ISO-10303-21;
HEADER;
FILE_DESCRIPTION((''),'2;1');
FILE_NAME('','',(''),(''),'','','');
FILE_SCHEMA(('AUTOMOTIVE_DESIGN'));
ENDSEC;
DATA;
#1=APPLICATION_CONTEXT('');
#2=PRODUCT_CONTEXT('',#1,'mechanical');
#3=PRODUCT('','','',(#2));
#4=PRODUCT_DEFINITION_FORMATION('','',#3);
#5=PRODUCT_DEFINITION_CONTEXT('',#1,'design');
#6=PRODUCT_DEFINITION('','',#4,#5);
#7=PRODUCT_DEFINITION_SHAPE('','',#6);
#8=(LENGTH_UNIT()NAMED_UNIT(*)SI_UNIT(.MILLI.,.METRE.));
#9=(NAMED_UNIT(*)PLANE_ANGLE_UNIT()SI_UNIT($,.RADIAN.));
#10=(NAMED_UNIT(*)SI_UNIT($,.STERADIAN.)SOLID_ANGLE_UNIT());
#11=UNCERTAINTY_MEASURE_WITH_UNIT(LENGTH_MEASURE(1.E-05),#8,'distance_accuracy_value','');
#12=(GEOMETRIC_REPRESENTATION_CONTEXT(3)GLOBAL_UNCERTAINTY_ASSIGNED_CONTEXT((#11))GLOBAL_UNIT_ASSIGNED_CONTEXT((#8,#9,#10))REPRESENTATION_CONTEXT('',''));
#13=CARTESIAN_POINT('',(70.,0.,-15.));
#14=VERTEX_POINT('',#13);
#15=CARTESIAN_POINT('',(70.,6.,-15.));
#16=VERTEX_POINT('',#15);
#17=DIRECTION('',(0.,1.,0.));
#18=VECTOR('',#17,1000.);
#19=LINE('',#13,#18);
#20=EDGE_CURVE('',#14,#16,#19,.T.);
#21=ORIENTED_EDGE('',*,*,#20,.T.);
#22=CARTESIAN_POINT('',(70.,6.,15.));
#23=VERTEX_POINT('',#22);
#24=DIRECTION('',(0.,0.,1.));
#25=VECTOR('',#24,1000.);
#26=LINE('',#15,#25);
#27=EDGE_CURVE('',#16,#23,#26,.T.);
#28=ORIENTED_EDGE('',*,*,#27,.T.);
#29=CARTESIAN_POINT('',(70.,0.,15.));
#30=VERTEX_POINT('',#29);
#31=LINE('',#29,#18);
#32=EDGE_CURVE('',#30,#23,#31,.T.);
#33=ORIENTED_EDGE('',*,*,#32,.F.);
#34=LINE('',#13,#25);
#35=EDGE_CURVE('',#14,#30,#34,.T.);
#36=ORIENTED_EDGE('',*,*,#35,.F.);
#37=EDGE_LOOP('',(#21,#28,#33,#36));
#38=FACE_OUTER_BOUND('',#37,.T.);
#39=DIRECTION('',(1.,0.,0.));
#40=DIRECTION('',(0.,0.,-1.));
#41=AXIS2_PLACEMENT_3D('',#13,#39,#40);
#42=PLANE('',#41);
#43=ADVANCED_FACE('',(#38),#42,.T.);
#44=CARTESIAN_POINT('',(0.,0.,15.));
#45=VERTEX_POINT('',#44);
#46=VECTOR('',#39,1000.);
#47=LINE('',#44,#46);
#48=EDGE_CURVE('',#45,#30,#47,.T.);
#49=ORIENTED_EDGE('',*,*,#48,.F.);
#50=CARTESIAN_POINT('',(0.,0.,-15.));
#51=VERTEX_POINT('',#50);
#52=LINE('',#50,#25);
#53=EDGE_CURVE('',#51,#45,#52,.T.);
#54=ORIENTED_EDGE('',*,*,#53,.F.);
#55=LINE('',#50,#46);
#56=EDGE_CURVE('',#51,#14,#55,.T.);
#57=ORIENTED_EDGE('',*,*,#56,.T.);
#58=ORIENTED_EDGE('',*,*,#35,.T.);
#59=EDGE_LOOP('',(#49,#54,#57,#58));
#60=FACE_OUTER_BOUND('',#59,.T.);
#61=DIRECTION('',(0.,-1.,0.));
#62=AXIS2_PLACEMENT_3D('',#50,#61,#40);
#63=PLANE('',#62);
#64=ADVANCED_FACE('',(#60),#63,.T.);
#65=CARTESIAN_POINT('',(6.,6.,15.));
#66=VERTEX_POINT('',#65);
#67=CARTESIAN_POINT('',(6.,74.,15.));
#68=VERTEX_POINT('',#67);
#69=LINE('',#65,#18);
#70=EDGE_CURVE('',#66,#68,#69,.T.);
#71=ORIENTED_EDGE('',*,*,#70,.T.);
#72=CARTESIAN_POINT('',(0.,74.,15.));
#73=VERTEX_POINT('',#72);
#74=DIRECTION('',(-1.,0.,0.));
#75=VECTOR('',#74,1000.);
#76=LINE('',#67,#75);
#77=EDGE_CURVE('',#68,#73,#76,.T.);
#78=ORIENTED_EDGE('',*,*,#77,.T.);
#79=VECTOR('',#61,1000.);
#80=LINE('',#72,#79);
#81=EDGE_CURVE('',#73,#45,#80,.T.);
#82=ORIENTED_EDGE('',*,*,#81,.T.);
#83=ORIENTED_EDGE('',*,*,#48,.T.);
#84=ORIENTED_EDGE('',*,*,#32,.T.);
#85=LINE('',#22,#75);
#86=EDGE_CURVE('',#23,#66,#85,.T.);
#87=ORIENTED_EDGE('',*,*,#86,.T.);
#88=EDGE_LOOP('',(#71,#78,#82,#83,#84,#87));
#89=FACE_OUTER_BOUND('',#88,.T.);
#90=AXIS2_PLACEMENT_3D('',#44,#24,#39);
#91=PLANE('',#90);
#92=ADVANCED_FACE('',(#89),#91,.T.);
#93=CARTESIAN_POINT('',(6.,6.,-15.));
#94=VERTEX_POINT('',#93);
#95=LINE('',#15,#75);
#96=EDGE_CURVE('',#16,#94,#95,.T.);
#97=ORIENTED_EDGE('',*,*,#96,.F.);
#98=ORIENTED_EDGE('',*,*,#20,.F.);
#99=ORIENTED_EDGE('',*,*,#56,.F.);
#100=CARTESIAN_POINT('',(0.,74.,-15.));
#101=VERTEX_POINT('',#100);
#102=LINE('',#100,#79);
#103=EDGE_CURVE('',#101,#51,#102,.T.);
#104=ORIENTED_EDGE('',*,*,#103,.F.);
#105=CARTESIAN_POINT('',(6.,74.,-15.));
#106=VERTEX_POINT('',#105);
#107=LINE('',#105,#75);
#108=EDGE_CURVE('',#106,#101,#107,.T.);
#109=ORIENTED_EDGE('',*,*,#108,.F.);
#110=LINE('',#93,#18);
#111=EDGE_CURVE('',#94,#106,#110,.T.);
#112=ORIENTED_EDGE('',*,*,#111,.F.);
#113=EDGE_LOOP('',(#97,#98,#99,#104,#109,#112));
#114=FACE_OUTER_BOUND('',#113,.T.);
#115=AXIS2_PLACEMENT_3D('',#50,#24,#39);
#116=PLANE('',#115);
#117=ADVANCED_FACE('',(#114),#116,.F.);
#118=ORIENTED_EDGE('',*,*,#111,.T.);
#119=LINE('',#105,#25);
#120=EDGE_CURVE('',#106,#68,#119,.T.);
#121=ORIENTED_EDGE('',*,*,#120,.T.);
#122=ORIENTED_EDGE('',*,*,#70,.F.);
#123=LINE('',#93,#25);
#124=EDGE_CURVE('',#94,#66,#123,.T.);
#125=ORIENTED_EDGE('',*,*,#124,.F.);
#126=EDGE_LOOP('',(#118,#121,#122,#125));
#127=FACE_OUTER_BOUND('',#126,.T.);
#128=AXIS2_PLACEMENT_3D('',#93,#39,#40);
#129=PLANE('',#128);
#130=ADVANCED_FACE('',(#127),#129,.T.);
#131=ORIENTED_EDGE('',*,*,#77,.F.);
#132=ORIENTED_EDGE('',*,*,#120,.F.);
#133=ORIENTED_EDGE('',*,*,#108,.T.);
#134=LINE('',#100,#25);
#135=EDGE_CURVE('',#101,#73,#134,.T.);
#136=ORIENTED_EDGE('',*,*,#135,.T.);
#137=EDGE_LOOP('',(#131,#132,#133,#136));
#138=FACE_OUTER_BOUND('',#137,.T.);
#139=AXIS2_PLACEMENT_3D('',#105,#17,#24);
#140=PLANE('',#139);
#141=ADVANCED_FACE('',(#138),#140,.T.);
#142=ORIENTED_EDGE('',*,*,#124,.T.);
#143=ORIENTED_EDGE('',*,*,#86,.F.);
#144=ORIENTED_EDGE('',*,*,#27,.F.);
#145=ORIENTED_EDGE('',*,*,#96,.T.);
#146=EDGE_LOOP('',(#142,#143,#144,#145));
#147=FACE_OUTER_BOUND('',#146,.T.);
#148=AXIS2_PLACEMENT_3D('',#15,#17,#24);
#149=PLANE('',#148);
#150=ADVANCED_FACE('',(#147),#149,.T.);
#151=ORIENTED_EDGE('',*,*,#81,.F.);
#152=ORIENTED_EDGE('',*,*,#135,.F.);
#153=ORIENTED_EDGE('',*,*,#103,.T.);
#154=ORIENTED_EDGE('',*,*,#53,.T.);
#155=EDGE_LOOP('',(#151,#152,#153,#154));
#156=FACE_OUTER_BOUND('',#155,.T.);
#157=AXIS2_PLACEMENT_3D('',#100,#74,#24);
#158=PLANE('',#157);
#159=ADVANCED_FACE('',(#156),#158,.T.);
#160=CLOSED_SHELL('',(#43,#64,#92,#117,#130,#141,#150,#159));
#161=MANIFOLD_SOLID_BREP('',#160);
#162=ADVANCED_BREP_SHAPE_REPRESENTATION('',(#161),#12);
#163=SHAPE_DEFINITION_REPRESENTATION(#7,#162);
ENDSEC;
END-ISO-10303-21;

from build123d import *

# Parameters (mm, degrees)
EXTRUDE_1_DEPTH = 15


with BuildPart() as part:
    # 草图1 → 凸台-拉伸1 (new, symmetric)
    with BuildSketch(Plane.XY):
        Polygon((0, 0), (70, 0), (70, 6), (6, 6), (6, 74), (0, 74), align=None)
    extrude(amount=EXTRUDE_1_DEPTH, both=True)


solid = part.part
